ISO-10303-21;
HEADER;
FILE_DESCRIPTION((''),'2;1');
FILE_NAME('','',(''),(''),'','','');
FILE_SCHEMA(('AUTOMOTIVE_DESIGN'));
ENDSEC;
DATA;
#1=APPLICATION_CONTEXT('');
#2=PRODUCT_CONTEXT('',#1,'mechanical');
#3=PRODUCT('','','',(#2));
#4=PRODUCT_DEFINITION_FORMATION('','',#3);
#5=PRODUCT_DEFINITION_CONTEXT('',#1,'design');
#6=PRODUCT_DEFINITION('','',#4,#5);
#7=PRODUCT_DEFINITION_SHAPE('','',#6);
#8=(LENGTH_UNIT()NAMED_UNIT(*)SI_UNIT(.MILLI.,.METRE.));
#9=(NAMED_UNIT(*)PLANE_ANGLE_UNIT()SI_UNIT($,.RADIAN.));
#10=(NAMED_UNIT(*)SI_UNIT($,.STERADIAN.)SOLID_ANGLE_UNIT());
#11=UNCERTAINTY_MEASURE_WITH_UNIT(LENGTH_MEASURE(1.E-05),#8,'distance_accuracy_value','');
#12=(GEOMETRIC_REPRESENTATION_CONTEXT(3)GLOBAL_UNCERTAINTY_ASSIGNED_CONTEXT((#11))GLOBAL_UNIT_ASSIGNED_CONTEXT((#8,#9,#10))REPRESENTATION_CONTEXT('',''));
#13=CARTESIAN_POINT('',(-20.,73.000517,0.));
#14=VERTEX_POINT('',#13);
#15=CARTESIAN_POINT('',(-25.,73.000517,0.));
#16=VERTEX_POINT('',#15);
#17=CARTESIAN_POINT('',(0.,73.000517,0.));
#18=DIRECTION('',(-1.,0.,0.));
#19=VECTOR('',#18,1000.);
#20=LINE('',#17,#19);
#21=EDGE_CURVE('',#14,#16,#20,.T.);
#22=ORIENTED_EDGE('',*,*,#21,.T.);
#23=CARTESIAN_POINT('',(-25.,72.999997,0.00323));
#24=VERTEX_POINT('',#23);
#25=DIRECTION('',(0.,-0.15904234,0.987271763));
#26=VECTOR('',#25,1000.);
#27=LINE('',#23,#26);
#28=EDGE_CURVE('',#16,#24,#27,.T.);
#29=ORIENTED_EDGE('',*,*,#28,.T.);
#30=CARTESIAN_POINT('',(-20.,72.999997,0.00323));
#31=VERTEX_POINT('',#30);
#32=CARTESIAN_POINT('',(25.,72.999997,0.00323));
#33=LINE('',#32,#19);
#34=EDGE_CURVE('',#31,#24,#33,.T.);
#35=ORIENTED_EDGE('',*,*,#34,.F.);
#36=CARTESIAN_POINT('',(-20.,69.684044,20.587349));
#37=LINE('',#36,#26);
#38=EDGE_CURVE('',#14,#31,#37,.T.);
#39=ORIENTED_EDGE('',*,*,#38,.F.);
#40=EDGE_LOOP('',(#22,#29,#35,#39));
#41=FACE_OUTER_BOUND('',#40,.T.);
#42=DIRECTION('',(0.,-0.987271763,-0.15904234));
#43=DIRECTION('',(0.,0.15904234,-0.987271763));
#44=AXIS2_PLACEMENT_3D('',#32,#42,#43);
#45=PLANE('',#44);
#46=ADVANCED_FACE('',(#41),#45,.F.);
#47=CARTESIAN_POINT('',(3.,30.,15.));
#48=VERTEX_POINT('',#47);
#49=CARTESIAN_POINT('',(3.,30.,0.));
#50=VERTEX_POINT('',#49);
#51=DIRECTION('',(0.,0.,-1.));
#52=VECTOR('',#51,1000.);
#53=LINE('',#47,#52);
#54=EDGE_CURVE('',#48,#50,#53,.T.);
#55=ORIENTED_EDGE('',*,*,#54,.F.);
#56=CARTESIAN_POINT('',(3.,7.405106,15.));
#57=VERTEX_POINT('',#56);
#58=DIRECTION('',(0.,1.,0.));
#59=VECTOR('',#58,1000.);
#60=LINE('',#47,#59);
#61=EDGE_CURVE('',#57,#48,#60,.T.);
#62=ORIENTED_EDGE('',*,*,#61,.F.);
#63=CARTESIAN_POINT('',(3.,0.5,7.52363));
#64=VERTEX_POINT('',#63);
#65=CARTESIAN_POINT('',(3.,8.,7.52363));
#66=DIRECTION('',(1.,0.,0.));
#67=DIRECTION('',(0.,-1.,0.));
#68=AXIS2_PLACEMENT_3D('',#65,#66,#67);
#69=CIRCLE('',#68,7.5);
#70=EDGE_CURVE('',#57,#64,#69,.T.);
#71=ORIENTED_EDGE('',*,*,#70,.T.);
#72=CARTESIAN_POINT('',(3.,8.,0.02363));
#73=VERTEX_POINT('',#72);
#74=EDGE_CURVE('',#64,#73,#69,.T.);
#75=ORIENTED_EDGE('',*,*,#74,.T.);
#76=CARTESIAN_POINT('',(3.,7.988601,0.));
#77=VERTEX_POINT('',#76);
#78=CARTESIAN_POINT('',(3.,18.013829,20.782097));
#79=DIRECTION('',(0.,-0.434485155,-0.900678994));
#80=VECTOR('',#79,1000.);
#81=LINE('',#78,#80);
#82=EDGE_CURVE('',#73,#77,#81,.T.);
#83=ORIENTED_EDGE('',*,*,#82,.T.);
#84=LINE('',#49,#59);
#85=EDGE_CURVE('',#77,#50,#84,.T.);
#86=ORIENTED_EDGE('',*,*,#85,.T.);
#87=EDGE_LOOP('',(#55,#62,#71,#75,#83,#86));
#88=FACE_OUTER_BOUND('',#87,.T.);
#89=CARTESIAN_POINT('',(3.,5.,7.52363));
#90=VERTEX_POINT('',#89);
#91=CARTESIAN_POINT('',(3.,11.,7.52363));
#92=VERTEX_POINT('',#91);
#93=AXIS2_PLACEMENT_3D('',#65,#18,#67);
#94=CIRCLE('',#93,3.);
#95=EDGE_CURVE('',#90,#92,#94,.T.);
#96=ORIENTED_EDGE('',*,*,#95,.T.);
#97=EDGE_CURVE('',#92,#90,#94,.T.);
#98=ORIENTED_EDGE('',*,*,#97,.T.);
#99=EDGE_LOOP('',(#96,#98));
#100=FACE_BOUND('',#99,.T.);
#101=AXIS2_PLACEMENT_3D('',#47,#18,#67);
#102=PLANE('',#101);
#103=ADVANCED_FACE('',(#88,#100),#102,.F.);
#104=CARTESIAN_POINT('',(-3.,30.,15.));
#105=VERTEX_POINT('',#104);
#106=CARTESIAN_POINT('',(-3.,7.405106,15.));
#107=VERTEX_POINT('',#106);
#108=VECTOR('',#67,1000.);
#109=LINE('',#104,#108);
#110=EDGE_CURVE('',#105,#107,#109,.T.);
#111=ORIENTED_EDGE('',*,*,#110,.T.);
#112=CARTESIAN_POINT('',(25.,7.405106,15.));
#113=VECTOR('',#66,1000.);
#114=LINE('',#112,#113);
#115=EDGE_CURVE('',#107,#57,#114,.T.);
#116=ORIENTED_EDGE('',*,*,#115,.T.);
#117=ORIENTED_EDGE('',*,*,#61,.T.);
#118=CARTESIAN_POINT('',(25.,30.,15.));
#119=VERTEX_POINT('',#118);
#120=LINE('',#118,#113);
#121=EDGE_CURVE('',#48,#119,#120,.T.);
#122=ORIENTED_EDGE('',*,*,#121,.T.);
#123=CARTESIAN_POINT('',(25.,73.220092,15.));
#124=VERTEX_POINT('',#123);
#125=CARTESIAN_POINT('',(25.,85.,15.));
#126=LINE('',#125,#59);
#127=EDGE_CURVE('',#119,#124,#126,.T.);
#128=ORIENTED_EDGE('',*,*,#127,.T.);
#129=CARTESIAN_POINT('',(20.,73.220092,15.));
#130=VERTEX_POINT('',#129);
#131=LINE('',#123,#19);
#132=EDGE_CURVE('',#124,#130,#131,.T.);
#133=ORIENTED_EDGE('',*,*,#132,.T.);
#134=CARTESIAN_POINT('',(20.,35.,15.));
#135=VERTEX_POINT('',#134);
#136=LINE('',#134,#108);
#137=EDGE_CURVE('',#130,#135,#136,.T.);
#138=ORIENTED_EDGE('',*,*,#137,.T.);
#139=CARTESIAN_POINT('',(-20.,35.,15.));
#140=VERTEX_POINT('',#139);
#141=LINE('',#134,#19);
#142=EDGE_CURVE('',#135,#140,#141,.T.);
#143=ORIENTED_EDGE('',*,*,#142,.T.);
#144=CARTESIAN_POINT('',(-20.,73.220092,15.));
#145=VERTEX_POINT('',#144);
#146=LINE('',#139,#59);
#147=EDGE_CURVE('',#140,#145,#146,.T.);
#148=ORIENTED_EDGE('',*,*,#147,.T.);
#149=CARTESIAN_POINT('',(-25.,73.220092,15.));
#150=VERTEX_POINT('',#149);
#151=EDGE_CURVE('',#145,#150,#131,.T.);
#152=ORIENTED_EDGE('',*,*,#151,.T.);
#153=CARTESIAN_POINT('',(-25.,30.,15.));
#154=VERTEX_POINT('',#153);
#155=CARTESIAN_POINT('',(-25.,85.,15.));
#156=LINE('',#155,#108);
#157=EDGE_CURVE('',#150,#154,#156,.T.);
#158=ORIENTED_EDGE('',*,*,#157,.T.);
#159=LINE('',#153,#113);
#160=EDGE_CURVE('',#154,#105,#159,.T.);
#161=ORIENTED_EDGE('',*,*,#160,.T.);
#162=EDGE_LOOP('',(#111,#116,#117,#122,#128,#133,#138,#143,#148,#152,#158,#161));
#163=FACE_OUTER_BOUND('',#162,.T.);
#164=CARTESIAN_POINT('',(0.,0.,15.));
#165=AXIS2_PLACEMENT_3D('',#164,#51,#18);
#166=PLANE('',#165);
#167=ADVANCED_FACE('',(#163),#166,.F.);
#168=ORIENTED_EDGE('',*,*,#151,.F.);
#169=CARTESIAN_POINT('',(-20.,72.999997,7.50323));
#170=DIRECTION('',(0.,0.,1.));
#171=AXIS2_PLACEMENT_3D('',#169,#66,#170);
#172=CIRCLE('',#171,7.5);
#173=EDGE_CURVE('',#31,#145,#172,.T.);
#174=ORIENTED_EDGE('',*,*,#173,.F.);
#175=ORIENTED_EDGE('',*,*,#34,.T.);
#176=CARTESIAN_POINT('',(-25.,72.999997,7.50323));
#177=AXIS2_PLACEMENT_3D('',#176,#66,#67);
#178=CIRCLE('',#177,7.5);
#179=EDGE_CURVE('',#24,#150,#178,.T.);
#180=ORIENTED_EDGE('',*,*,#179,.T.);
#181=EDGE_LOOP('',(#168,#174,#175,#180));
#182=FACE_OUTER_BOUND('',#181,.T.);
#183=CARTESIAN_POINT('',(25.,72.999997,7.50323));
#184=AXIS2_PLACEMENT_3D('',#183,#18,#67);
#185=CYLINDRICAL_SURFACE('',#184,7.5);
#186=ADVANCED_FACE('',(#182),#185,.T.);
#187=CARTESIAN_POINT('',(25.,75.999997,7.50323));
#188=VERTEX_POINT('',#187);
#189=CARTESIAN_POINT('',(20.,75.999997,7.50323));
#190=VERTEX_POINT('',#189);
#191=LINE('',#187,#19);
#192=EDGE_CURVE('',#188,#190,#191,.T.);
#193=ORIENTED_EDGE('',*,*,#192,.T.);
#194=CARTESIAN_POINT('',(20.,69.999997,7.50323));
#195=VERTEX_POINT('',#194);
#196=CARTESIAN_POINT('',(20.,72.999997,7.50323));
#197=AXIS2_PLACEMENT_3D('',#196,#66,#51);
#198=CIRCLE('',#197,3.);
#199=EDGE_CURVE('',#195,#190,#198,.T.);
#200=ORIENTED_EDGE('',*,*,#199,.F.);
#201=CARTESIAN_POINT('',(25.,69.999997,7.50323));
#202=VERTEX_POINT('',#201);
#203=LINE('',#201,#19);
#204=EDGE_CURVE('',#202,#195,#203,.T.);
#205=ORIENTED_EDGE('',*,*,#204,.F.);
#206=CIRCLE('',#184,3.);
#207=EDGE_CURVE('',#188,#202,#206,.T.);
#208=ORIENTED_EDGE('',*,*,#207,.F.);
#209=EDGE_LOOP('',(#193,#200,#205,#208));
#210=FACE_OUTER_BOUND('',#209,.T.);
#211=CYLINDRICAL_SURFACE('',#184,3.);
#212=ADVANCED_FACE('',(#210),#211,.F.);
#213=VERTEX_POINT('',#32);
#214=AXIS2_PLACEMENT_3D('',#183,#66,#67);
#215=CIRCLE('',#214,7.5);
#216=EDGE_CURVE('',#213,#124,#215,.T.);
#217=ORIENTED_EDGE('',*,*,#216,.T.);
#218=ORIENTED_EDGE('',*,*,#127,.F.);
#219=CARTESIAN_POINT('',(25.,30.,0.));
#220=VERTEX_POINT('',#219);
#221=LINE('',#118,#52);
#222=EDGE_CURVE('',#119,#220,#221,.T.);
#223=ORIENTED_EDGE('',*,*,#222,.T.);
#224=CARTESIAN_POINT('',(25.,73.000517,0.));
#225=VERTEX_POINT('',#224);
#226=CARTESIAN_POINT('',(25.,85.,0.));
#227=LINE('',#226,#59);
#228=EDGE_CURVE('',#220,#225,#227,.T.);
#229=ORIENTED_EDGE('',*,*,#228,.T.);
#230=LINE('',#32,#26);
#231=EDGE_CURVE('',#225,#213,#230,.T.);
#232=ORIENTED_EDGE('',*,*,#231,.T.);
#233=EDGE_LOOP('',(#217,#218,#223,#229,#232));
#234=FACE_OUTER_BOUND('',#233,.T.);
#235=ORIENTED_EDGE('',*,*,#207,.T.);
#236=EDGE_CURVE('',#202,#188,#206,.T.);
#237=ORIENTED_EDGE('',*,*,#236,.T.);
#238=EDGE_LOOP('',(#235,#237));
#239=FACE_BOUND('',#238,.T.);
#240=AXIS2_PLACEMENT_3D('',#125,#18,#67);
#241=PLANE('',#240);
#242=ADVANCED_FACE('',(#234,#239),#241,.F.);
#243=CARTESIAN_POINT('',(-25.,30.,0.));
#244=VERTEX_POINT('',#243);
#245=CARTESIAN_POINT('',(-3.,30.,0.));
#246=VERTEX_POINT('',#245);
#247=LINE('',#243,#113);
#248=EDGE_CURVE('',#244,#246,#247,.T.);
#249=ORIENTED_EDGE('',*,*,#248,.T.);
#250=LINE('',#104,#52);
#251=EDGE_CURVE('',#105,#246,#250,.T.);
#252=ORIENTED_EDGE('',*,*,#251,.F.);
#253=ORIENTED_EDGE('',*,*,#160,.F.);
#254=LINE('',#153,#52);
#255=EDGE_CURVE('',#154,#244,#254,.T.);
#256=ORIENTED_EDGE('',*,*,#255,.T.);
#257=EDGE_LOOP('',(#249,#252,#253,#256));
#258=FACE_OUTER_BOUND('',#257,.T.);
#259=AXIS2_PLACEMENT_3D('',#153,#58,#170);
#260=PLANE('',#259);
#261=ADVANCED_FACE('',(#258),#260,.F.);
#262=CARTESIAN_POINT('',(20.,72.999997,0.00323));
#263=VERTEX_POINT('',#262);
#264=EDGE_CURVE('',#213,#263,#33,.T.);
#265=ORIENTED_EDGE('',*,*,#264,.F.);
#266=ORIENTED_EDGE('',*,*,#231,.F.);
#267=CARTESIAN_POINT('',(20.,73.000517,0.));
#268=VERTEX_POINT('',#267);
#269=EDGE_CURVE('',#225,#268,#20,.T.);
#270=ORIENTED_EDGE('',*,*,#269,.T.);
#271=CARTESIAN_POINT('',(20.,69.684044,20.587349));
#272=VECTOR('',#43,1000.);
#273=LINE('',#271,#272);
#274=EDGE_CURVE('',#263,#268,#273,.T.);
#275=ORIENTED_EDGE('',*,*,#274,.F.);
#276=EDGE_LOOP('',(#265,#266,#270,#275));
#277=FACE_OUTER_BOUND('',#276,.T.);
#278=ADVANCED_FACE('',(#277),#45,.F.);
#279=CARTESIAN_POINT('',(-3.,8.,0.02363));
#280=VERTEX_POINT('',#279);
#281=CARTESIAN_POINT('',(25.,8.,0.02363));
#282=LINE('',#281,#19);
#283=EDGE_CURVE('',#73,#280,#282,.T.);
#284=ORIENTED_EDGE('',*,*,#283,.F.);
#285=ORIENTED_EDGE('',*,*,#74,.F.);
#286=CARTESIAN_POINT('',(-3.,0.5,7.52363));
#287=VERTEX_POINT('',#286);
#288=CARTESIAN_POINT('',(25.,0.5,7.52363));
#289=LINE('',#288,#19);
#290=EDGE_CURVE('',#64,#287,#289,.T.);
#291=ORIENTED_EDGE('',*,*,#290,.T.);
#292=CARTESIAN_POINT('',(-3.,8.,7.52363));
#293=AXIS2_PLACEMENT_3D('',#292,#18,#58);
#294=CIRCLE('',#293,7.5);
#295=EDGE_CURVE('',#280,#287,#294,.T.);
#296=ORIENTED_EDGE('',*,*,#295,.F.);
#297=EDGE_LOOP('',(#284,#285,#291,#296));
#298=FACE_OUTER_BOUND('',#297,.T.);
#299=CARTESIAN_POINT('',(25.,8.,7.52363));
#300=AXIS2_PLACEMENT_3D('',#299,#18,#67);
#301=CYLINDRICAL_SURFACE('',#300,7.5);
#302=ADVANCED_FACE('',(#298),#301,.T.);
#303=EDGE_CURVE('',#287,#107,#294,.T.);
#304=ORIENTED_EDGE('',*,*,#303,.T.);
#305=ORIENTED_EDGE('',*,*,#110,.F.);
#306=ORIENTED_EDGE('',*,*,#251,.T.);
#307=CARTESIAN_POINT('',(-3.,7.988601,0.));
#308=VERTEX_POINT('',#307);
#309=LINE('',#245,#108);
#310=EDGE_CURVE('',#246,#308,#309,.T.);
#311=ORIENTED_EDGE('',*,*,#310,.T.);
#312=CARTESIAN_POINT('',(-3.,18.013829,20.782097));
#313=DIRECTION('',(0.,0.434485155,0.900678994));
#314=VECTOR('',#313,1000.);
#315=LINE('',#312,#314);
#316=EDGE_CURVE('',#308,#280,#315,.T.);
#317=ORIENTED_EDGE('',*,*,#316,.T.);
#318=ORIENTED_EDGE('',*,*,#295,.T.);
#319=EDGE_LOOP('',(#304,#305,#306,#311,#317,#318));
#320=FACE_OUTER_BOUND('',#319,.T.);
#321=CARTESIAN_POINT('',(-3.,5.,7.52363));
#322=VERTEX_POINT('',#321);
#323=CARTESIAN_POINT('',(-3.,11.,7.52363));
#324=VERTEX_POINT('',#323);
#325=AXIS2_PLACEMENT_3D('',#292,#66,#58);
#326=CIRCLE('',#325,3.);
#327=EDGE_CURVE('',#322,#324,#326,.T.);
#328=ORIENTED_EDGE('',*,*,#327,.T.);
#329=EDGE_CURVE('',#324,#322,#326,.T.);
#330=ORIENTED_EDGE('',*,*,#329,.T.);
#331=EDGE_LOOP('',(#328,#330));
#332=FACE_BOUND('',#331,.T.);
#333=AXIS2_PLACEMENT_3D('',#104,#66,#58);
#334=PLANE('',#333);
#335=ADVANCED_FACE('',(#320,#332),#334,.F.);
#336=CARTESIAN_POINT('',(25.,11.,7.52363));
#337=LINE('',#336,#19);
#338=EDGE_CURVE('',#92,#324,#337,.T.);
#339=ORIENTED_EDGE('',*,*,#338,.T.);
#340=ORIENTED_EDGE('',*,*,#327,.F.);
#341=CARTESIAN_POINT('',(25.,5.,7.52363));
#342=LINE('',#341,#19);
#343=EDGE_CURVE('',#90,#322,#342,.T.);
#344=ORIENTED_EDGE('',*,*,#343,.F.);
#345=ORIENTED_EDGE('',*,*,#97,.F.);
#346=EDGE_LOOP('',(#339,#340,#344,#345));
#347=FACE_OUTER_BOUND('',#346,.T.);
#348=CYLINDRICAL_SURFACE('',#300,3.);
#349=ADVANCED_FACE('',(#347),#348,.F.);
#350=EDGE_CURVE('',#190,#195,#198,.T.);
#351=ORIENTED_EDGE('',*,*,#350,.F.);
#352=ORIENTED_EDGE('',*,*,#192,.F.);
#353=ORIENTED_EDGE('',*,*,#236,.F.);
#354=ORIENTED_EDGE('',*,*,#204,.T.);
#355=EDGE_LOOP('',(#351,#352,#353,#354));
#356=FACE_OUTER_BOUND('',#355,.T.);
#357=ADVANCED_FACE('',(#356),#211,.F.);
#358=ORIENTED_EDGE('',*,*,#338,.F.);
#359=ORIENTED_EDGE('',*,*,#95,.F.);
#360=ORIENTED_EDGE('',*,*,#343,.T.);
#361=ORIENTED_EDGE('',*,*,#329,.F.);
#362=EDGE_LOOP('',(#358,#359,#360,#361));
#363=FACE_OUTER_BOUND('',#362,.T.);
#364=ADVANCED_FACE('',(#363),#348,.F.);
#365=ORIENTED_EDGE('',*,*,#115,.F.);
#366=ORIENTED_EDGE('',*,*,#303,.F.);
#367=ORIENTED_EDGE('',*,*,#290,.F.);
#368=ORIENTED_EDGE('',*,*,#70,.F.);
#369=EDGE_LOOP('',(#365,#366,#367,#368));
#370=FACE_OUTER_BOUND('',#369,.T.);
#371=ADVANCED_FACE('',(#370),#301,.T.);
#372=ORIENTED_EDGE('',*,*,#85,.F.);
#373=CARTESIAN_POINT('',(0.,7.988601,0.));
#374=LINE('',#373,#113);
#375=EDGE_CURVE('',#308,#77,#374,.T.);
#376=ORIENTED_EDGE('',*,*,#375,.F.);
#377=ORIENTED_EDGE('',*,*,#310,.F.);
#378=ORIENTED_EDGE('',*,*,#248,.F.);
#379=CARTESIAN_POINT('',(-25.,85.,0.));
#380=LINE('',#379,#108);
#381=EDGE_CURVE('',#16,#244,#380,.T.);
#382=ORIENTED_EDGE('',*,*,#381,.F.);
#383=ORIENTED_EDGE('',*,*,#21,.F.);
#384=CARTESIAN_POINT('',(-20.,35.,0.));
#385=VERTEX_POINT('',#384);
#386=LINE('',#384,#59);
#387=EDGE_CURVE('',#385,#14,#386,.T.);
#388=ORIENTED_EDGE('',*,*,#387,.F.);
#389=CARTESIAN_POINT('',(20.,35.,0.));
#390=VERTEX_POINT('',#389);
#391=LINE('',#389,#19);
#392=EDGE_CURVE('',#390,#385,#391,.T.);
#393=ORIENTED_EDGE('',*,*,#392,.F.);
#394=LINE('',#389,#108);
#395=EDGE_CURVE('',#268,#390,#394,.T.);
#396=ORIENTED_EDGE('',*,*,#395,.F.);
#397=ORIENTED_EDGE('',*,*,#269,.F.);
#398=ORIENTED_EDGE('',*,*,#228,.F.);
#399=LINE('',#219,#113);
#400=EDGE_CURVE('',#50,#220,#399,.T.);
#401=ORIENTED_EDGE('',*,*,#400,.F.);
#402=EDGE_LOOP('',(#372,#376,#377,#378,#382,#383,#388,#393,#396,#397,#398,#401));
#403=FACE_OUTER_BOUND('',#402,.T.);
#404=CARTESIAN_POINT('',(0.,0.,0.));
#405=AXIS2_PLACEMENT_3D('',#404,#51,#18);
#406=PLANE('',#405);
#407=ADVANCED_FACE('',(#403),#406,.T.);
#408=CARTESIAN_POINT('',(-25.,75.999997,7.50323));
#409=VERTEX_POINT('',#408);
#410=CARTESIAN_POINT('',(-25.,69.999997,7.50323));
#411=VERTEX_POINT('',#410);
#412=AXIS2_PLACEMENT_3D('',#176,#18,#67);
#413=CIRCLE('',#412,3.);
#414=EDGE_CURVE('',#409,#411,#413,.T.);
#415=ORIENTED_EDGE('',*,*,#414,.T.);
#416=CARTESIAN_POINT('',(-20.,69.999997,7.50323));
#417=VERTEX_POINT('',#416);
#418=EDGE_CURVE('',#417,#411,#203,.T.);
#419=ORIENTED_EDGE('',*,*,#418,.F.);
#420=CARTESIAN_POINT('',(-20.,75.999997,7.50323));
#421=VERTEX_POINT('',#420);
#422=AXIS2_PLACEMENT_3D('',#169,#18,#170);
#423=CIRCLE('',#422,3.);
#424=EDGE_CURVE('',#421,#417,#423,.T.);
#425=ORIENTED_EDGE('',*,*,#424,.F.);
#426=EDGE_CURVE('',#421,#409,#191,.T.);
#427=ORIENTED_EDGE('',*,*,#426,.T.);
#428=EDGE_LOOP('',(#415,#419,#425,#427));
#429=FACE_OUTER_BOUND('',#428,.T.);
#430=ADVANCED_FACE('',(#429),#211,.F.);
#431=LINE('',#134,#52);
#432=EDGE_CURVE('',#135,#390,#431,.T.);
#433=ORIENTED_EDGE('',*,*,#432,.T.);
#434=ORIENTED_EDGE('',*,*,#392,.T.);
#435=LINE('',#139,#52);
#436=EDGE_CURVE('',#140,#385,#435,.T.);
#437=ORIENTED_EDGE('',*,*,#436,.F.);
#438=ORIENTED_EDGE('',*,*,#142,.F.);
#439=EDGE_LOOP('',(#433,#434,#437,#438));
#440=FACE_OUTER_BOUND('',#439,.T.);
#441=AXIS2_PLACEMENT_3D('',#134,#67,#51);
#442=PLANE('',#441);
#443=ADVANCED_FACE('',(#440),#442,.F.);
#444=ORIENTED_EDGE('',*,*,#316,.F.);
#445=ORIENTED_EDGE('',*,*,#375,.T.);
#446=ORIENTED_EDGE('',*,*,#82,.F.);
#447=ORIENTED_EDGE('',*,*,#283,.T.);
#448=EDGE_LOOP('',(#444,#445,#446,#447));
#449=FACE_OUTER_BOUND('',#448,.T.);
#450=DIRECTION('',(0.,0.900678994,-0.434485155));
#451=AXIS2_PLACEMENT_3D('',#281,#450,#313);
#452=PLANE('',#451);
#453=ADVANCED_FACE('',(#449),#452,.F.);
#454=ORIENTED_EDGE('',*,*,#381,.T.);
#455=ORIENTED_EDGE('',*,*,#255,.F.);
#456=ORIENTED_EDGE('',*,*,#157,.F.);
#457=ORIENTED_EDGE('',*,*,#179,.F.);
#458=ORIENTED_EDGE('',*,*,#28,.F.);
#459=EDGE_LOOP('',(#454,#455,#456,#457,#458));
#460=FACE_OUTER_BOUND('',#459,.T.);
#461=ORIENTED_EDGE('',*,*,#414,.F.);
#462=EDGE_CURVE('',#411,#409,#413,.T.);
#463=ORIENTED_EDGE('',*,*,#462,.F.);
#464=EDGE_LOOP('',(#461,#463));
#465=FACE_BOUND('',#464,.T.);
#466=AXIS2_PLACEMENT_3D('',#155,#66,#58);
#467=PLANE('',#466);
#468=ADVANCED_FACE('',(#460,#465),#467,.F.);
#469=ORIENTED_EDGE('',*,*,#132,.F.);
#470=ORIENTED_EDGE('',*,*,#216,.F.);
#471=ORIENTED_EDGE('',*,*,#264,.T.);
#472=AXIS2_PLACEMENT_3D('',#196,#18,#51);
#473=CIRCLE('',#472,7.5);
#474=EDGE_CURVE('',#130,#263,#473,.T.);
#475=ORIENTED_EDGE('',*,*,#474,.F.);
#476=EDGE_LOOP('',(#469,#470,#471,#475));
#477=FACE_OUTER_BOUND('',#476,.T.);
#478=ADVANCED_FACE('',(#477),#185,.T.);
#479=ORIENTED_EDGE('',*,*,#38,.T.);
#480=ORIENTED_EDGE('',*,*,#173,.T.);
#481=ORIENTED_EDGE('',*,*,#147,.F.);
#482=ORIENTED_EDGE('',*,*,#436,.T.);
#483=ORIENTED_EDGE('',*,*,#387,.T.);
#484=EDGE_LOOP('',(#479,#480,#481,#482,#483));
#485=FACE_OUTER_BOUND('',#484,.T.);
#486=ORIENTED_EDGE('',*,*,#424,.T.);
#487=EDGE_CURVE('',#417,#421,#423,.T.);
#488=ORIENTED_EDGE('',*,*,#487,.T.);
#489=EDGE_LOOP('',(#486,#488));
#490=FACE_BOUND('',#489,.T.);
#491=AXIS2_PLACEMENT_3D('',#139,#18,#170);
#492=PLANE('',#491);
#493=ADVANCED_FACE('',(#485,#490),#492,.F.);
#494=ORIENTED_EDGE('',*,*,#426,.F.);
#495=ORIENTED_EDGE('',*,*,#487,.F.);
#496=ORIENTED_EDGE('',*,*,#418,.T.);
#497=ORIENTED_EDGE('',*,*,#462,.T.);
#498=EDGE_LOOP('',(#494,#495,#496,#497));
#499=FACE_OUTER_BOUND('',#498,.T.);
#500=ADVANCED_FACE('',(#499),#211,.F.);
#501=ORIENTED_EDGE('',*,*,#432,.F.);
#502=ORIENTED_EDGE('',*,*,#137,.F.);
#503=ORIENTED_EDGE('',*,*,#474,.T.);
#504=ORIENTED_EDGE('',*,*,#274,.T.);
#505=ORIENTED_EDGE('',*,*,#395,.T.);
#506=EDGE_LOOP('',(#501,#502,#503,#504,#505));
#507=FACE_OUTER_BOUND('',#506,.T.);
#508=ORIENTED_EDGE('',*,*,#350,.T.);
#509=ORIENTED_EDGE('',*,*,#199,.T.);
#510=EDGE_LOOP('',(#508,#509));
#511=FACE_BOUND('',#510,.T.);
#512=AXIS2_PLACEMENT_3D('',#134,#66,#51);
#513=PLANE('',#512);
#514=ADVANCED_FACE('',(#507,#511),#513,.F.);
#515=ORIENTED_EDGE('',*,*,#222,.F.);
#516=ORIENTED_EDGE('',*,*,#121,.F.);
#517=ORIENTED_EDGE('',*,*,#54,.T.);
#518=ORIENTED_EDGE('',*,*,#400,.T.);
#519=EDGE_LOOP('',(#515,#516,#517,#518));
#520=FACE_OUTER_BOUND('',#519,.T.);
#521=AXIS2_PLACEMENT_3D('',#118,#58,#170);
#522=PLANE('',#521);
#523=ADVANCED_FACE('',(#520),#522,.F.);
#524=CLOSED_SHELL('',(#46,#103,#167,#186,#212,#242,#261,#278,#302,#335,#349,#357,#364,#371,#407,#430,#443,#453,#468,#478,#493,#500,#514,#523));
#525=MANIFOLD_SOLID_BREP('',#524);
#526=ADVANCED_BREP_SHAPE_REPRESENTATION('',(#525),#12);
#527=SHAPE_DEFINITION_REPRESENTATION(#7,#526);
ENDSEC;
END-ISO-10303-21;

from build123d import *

# Parameters (mm, degrees)
BOSS_EXTRUDE1_DEPTH = 15
SKETCH2_R           = 3
CUT_EXTRUDE1_DEPTH  = 100.749686716


with BuildPart() as part:
    # Sketch1 → Boss-Extrude1 (new body)
    with BuildSketch(Plane.XY):
        Polygon((20, 35), (-20, 35), (-20, 85), (-25, 85), (-25, 30), (-3, 30), (-3, 0), (0, 0), (3, 0), (3, 30), (25, 30), (25, 85), (20, 85), align=None)
    extrude(amount=BOSS_EXTRUDE1_DEPTH)

    # Sketch2 → Cut-Extrude1 (cut, through all)
    with BuildSketch(Plane.ZY.offset(25)):
        with Locations(Location((7.503230167, 72.999996799, 0), (0, 0, 270))):
            Circle(SKETCH2_R)
        with Locations(Location((7.523630467, 8, 0), (0, 0, 270))):
            Circle(SKETCH2_R)
        with BuildLine():
            Line((0.003230167, 72.999996799), (-23.0886588, 76.719933094))
            Line((-23.0886588, 76.719933094), (-0.661840838, 109.961720022))
            Line((-0.661840838, 109.961720022), (34.957913296, 90.556615978))
            Line((34.957913296, 90.556615978), (15.003230167, 72.999996799))
            ThreePointArc((15.003230167, 72.999996799), (7.503230167, 80.499996799), (0.003230167, 72.999996799))
        make_face()
        with BuildLine():
            Line((0.023630467, 8), (-15.301630232, 0.607134927))
            Line((-15.301630232, 0.607134927), (-3.280552195, -15.592363972))
            Line((-3.280552195, -15.592363972), (32.469088575, -12.351899457))
            Line((32.469088575, -12.351899457), (24.841547467, 4.357134927))
            Line((24.841547467, 4.357134927), (15.023630467, 8))
            ThreePointArc((15.023630467, 8), (7.523630467, 0.5), (0.023630467, 8))
        make_face()
    extrude(amount=-CUT_EXTRUDE1_DEPTH, mode=Mode.SUBTRACT)


solid = part.part
